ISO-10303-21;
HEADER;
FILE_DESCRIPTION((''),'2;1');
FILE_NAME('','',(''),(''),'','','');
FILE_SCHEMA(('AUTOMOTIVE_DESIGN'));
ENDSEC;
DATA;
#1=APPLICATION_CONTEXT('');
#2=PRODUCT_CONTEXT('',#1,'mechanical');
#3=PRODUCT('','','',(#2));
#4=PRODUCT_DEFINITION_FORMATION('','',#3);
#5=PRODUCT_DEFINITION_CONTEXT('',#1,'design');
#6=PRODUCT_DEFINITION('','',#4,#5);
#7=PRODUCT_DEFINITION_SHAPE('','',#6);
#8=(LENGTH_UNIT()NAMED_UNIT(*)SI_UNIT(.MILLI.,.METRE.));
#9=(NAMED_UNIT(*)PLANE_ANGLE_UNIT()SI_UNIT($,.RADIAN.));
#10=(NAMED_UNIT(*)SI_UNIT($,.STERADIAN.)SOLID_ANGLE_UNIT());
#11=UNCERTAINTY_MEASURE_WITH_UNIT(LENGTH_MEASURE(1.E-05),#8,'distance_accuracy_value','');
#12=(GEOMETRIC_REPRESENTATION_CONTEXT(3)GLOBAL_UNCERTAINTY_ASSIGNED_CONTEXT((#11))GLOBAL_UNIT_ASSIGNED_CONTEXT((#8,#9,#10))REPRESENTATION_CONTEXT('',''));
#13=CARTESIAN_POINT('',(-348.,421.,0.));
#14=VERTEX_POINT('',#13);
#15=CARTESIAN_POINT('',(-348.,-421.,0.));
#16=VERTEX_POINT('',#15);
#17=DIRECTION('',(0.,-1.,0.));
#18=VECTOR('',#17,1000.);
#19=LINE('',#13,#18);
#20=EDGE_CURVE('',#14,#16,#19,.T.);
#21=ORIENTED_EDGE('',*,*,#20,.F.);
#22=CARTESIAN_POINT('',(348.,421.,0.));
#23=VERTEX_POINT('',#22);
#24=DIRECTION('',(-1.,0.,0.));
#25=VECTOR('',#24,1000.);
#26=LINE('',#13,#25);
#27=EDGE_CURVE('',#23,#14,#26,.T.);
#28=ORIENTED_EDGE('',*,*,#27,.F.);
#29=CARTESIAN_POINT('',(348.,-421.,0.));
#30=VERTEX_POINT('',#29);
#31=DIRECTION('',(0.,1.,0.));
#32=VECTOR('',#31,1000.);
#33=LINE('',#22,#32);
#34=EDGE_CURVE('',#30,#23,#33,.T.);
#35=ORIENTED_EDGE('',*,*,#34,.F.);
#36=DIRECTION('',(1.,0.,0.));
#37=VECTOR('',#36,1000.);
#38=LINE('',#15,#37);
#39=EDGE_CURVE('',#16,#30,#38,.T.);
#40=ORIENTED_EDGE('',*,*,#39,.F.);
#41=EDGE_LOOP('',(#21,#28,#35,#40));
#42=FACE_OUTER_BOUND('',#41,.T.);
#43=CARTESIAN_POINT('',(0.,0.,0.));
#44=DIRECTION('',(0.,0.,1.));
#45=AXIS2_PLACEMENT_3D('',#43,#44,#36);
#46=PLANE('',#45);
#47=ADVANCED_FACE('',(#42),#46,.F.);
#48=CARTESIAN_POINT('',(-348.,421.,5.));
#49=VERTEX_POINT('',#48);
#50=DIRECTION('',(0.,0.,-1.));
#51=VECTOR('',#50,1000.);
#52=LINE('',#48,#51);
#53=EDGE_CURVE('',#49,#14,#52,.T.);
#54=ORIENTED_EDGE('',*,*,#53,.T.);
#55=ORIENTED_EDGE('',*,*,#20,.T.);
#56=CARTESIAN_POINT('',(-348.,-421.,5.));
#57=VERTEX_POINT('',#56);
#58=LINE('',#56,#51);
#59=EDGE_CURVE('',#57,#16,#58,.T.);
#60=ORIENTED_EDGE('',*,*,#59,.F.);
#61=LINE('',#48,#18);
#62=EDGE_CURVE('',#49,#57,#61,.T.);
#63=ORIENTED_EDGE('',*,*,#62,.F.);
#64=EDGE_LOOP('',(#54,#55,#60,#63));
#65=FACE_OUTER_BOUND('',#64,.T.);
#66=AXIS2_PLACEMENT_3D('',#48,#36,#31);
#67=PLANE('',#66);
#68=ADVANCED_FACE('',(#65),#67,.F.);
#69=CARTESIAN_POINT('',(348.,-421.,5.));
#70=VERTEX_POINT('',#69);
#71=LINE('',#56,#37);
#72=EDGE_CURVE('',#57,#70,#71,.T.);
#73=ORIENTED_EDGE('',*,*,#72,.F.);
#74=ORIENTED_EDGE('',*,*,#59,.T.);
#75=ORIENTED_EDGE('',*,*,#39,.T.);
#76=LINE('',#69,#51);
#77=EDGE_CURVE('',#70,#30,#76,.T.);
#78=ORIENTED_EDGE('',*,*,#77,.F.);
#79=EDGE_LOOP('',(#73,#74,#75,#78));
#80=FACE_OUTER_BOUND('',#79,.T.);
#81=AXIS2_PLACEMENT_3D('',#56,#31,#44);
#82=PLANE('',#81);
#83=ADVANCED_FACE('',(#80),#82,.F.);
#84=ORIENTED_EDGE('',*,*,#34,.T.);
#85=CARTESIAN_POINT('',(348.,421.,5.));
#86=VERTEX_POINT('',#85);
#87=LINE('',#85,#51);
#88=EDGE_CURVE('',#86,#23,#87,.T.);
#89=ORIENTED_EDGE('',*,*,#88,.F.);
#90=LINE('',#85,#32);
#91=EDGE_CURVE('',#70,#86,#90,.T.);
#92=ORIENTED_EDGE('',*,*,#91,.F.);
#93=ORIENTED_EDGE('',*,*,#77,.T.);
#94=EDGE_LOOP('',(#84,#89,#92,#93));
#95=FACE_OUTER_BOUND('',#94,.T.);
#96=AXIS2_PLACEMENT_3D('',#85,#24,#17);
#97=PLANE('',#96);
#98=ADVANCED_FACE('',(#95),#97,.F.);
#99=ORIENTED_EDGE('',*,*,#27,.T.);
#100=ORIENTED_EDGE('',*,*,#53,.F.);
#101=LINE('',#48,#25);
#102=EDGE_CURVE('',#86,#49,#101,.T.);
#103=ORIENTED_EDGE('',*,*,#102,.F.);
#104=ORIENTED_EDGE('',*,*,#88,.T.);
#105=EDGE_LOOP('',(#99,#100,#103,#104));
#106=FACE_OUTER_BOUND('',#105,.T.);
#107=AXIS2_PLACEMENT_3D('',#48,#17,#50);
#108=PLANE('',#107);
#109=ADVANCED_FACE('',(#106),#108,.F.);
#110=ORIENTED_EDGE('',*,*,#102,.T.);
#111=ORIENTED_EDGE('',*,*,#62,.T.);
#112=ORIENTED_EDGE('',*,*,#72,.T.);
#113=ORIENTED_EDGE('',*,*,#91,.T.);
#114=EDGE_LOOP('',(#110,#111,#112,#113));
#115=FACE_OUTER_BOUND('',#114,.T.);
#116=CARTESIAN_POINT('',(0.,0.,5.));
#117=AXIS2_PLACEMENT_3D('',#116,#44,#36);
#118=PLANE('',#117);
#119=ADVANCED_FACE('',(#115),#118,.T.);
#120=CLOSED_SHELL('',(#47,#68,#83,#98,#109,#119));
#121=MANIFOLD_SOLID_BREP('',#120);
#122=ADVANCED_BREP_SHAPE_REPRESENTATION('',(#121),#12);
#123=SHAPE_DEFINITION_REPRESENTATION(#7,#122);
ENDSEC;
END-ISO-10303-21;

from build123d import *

# Parameters (mm, degrees)
SKETCH_1_W      = 696
SKETCH_1_H      = 842
EXTRUDE_1_DEPTH = 5


with BuildPart() as part:
    # 草图1 → 凸台-拉伸1 (new body)
    with BuildSketch(Plane.XY):
        Rectangle(SKETCH_1_W, SKETCH_1_H)
    extrude(amount=EXTRUDE_1_DEPTH)


solid = part.part
